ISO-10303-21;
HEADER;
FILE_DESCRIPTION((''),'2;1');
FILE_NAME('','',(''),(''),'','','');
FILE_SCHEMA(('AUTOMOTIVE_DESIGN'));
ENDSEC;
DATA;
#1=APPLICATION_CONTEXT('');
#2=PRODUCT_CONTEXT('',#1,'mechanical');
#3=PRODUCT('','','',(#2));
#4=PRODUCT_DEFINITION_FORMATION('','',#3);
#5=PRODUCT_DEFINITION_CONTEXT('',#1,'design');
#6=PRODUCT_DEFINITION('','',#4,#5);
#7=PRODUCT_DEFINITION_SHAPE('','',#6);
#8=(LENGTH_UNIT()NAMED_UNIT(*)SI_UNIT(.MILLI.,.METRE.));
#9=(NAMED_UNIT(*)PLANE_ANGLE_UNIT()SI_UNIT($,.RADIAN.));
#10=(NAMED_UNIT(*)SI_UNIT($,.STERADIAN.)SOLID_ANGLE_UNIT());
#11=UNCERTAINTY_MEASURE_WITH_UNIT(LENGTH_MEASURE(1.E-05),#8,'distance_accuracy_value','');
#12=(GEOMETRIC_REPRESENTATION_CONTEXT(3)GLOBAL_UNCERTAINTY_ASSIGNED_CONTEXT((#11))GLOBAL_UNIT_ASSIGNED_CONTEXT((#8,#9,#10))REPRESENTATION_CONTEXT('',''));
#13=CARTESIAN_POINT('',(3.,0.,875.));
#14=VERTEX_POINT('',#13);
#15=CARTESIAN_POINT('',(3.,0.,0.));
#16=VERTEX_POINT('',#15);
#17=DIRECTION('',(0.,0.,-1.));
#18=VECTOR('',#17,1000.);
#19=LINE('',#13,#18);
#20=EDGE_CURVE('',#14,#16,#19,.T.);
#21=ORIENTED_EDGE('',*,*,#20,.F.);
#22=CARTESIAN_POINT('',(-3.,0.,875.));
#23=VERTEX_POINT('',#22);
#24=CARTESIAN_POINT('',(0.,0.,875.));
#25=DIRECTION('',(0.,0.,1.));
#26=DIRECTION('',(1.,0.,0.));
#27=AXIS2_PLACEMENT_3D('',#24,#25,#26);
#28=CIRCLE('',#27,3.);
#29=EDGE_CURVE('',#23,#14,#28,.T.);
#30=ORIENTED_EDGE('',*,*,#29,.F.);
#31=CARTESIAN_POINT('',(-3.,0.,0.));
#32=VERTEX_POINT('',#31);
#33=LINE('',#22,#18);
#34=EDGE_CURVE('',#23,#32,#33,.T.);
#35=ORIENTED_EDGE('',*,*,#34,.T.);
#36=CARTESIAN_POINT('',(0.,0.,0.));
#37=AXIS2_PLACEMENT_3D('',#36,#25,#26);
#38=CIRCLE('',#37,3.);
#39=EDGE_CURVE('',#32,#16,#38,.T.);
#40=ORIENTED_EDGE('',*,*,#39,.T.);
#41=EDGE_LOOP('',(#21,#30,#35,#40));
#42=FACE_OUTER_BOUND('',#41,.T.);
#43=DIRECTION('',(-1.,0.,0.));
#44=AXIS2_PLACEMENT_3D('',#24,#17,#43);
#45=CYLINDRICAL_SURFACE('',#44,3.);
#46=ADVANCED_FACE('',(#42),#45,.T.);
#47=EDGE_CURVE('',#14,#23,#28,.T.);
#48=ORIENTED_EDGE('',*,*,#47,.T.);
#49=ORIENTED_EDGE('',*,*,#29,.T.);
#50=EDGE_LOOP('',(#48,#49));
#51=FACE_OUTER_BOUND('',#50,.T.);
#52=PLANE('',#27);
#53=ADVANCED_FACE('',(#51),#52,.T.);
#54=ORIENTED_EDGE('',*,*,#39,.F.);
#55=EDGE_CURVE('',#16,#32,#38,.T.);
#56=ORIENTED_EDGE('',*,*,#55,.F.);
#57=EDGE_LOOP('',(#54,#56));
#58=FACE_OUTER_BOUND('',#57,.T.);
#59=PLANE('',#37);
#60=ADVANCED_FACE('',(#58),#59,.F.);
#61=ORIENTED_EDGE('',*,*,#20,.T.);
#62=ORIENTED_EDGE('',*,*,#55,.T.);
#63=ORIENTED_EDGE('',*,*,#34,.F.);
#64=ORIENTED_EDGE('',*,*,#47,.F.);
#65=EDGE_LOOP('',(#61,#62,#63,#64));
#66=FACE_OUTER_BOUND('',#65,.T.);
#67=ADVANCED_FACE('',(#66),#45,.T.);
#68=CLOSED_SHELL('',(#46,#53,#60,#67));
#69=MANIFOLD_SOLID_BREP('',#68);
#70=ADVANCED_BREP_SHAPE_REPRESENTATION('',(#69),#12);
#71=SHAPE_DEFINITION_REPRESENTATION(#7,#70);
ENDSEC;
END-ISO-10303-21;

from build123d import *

# Parameters (mm, degrees)
SKETCH1_R           = 3
BOSS_EXTRUDE1_DEPTH = 875


with BuildPart() as part:
    # Sketch1 → Boss-Extrude1 (new body)
    with BuildSketch(Plane.XY):
        Circle(SKETCH1_R)
    extrude(amount=BOSS_EXTRUDE1_DEPTH)


solid = part.part
